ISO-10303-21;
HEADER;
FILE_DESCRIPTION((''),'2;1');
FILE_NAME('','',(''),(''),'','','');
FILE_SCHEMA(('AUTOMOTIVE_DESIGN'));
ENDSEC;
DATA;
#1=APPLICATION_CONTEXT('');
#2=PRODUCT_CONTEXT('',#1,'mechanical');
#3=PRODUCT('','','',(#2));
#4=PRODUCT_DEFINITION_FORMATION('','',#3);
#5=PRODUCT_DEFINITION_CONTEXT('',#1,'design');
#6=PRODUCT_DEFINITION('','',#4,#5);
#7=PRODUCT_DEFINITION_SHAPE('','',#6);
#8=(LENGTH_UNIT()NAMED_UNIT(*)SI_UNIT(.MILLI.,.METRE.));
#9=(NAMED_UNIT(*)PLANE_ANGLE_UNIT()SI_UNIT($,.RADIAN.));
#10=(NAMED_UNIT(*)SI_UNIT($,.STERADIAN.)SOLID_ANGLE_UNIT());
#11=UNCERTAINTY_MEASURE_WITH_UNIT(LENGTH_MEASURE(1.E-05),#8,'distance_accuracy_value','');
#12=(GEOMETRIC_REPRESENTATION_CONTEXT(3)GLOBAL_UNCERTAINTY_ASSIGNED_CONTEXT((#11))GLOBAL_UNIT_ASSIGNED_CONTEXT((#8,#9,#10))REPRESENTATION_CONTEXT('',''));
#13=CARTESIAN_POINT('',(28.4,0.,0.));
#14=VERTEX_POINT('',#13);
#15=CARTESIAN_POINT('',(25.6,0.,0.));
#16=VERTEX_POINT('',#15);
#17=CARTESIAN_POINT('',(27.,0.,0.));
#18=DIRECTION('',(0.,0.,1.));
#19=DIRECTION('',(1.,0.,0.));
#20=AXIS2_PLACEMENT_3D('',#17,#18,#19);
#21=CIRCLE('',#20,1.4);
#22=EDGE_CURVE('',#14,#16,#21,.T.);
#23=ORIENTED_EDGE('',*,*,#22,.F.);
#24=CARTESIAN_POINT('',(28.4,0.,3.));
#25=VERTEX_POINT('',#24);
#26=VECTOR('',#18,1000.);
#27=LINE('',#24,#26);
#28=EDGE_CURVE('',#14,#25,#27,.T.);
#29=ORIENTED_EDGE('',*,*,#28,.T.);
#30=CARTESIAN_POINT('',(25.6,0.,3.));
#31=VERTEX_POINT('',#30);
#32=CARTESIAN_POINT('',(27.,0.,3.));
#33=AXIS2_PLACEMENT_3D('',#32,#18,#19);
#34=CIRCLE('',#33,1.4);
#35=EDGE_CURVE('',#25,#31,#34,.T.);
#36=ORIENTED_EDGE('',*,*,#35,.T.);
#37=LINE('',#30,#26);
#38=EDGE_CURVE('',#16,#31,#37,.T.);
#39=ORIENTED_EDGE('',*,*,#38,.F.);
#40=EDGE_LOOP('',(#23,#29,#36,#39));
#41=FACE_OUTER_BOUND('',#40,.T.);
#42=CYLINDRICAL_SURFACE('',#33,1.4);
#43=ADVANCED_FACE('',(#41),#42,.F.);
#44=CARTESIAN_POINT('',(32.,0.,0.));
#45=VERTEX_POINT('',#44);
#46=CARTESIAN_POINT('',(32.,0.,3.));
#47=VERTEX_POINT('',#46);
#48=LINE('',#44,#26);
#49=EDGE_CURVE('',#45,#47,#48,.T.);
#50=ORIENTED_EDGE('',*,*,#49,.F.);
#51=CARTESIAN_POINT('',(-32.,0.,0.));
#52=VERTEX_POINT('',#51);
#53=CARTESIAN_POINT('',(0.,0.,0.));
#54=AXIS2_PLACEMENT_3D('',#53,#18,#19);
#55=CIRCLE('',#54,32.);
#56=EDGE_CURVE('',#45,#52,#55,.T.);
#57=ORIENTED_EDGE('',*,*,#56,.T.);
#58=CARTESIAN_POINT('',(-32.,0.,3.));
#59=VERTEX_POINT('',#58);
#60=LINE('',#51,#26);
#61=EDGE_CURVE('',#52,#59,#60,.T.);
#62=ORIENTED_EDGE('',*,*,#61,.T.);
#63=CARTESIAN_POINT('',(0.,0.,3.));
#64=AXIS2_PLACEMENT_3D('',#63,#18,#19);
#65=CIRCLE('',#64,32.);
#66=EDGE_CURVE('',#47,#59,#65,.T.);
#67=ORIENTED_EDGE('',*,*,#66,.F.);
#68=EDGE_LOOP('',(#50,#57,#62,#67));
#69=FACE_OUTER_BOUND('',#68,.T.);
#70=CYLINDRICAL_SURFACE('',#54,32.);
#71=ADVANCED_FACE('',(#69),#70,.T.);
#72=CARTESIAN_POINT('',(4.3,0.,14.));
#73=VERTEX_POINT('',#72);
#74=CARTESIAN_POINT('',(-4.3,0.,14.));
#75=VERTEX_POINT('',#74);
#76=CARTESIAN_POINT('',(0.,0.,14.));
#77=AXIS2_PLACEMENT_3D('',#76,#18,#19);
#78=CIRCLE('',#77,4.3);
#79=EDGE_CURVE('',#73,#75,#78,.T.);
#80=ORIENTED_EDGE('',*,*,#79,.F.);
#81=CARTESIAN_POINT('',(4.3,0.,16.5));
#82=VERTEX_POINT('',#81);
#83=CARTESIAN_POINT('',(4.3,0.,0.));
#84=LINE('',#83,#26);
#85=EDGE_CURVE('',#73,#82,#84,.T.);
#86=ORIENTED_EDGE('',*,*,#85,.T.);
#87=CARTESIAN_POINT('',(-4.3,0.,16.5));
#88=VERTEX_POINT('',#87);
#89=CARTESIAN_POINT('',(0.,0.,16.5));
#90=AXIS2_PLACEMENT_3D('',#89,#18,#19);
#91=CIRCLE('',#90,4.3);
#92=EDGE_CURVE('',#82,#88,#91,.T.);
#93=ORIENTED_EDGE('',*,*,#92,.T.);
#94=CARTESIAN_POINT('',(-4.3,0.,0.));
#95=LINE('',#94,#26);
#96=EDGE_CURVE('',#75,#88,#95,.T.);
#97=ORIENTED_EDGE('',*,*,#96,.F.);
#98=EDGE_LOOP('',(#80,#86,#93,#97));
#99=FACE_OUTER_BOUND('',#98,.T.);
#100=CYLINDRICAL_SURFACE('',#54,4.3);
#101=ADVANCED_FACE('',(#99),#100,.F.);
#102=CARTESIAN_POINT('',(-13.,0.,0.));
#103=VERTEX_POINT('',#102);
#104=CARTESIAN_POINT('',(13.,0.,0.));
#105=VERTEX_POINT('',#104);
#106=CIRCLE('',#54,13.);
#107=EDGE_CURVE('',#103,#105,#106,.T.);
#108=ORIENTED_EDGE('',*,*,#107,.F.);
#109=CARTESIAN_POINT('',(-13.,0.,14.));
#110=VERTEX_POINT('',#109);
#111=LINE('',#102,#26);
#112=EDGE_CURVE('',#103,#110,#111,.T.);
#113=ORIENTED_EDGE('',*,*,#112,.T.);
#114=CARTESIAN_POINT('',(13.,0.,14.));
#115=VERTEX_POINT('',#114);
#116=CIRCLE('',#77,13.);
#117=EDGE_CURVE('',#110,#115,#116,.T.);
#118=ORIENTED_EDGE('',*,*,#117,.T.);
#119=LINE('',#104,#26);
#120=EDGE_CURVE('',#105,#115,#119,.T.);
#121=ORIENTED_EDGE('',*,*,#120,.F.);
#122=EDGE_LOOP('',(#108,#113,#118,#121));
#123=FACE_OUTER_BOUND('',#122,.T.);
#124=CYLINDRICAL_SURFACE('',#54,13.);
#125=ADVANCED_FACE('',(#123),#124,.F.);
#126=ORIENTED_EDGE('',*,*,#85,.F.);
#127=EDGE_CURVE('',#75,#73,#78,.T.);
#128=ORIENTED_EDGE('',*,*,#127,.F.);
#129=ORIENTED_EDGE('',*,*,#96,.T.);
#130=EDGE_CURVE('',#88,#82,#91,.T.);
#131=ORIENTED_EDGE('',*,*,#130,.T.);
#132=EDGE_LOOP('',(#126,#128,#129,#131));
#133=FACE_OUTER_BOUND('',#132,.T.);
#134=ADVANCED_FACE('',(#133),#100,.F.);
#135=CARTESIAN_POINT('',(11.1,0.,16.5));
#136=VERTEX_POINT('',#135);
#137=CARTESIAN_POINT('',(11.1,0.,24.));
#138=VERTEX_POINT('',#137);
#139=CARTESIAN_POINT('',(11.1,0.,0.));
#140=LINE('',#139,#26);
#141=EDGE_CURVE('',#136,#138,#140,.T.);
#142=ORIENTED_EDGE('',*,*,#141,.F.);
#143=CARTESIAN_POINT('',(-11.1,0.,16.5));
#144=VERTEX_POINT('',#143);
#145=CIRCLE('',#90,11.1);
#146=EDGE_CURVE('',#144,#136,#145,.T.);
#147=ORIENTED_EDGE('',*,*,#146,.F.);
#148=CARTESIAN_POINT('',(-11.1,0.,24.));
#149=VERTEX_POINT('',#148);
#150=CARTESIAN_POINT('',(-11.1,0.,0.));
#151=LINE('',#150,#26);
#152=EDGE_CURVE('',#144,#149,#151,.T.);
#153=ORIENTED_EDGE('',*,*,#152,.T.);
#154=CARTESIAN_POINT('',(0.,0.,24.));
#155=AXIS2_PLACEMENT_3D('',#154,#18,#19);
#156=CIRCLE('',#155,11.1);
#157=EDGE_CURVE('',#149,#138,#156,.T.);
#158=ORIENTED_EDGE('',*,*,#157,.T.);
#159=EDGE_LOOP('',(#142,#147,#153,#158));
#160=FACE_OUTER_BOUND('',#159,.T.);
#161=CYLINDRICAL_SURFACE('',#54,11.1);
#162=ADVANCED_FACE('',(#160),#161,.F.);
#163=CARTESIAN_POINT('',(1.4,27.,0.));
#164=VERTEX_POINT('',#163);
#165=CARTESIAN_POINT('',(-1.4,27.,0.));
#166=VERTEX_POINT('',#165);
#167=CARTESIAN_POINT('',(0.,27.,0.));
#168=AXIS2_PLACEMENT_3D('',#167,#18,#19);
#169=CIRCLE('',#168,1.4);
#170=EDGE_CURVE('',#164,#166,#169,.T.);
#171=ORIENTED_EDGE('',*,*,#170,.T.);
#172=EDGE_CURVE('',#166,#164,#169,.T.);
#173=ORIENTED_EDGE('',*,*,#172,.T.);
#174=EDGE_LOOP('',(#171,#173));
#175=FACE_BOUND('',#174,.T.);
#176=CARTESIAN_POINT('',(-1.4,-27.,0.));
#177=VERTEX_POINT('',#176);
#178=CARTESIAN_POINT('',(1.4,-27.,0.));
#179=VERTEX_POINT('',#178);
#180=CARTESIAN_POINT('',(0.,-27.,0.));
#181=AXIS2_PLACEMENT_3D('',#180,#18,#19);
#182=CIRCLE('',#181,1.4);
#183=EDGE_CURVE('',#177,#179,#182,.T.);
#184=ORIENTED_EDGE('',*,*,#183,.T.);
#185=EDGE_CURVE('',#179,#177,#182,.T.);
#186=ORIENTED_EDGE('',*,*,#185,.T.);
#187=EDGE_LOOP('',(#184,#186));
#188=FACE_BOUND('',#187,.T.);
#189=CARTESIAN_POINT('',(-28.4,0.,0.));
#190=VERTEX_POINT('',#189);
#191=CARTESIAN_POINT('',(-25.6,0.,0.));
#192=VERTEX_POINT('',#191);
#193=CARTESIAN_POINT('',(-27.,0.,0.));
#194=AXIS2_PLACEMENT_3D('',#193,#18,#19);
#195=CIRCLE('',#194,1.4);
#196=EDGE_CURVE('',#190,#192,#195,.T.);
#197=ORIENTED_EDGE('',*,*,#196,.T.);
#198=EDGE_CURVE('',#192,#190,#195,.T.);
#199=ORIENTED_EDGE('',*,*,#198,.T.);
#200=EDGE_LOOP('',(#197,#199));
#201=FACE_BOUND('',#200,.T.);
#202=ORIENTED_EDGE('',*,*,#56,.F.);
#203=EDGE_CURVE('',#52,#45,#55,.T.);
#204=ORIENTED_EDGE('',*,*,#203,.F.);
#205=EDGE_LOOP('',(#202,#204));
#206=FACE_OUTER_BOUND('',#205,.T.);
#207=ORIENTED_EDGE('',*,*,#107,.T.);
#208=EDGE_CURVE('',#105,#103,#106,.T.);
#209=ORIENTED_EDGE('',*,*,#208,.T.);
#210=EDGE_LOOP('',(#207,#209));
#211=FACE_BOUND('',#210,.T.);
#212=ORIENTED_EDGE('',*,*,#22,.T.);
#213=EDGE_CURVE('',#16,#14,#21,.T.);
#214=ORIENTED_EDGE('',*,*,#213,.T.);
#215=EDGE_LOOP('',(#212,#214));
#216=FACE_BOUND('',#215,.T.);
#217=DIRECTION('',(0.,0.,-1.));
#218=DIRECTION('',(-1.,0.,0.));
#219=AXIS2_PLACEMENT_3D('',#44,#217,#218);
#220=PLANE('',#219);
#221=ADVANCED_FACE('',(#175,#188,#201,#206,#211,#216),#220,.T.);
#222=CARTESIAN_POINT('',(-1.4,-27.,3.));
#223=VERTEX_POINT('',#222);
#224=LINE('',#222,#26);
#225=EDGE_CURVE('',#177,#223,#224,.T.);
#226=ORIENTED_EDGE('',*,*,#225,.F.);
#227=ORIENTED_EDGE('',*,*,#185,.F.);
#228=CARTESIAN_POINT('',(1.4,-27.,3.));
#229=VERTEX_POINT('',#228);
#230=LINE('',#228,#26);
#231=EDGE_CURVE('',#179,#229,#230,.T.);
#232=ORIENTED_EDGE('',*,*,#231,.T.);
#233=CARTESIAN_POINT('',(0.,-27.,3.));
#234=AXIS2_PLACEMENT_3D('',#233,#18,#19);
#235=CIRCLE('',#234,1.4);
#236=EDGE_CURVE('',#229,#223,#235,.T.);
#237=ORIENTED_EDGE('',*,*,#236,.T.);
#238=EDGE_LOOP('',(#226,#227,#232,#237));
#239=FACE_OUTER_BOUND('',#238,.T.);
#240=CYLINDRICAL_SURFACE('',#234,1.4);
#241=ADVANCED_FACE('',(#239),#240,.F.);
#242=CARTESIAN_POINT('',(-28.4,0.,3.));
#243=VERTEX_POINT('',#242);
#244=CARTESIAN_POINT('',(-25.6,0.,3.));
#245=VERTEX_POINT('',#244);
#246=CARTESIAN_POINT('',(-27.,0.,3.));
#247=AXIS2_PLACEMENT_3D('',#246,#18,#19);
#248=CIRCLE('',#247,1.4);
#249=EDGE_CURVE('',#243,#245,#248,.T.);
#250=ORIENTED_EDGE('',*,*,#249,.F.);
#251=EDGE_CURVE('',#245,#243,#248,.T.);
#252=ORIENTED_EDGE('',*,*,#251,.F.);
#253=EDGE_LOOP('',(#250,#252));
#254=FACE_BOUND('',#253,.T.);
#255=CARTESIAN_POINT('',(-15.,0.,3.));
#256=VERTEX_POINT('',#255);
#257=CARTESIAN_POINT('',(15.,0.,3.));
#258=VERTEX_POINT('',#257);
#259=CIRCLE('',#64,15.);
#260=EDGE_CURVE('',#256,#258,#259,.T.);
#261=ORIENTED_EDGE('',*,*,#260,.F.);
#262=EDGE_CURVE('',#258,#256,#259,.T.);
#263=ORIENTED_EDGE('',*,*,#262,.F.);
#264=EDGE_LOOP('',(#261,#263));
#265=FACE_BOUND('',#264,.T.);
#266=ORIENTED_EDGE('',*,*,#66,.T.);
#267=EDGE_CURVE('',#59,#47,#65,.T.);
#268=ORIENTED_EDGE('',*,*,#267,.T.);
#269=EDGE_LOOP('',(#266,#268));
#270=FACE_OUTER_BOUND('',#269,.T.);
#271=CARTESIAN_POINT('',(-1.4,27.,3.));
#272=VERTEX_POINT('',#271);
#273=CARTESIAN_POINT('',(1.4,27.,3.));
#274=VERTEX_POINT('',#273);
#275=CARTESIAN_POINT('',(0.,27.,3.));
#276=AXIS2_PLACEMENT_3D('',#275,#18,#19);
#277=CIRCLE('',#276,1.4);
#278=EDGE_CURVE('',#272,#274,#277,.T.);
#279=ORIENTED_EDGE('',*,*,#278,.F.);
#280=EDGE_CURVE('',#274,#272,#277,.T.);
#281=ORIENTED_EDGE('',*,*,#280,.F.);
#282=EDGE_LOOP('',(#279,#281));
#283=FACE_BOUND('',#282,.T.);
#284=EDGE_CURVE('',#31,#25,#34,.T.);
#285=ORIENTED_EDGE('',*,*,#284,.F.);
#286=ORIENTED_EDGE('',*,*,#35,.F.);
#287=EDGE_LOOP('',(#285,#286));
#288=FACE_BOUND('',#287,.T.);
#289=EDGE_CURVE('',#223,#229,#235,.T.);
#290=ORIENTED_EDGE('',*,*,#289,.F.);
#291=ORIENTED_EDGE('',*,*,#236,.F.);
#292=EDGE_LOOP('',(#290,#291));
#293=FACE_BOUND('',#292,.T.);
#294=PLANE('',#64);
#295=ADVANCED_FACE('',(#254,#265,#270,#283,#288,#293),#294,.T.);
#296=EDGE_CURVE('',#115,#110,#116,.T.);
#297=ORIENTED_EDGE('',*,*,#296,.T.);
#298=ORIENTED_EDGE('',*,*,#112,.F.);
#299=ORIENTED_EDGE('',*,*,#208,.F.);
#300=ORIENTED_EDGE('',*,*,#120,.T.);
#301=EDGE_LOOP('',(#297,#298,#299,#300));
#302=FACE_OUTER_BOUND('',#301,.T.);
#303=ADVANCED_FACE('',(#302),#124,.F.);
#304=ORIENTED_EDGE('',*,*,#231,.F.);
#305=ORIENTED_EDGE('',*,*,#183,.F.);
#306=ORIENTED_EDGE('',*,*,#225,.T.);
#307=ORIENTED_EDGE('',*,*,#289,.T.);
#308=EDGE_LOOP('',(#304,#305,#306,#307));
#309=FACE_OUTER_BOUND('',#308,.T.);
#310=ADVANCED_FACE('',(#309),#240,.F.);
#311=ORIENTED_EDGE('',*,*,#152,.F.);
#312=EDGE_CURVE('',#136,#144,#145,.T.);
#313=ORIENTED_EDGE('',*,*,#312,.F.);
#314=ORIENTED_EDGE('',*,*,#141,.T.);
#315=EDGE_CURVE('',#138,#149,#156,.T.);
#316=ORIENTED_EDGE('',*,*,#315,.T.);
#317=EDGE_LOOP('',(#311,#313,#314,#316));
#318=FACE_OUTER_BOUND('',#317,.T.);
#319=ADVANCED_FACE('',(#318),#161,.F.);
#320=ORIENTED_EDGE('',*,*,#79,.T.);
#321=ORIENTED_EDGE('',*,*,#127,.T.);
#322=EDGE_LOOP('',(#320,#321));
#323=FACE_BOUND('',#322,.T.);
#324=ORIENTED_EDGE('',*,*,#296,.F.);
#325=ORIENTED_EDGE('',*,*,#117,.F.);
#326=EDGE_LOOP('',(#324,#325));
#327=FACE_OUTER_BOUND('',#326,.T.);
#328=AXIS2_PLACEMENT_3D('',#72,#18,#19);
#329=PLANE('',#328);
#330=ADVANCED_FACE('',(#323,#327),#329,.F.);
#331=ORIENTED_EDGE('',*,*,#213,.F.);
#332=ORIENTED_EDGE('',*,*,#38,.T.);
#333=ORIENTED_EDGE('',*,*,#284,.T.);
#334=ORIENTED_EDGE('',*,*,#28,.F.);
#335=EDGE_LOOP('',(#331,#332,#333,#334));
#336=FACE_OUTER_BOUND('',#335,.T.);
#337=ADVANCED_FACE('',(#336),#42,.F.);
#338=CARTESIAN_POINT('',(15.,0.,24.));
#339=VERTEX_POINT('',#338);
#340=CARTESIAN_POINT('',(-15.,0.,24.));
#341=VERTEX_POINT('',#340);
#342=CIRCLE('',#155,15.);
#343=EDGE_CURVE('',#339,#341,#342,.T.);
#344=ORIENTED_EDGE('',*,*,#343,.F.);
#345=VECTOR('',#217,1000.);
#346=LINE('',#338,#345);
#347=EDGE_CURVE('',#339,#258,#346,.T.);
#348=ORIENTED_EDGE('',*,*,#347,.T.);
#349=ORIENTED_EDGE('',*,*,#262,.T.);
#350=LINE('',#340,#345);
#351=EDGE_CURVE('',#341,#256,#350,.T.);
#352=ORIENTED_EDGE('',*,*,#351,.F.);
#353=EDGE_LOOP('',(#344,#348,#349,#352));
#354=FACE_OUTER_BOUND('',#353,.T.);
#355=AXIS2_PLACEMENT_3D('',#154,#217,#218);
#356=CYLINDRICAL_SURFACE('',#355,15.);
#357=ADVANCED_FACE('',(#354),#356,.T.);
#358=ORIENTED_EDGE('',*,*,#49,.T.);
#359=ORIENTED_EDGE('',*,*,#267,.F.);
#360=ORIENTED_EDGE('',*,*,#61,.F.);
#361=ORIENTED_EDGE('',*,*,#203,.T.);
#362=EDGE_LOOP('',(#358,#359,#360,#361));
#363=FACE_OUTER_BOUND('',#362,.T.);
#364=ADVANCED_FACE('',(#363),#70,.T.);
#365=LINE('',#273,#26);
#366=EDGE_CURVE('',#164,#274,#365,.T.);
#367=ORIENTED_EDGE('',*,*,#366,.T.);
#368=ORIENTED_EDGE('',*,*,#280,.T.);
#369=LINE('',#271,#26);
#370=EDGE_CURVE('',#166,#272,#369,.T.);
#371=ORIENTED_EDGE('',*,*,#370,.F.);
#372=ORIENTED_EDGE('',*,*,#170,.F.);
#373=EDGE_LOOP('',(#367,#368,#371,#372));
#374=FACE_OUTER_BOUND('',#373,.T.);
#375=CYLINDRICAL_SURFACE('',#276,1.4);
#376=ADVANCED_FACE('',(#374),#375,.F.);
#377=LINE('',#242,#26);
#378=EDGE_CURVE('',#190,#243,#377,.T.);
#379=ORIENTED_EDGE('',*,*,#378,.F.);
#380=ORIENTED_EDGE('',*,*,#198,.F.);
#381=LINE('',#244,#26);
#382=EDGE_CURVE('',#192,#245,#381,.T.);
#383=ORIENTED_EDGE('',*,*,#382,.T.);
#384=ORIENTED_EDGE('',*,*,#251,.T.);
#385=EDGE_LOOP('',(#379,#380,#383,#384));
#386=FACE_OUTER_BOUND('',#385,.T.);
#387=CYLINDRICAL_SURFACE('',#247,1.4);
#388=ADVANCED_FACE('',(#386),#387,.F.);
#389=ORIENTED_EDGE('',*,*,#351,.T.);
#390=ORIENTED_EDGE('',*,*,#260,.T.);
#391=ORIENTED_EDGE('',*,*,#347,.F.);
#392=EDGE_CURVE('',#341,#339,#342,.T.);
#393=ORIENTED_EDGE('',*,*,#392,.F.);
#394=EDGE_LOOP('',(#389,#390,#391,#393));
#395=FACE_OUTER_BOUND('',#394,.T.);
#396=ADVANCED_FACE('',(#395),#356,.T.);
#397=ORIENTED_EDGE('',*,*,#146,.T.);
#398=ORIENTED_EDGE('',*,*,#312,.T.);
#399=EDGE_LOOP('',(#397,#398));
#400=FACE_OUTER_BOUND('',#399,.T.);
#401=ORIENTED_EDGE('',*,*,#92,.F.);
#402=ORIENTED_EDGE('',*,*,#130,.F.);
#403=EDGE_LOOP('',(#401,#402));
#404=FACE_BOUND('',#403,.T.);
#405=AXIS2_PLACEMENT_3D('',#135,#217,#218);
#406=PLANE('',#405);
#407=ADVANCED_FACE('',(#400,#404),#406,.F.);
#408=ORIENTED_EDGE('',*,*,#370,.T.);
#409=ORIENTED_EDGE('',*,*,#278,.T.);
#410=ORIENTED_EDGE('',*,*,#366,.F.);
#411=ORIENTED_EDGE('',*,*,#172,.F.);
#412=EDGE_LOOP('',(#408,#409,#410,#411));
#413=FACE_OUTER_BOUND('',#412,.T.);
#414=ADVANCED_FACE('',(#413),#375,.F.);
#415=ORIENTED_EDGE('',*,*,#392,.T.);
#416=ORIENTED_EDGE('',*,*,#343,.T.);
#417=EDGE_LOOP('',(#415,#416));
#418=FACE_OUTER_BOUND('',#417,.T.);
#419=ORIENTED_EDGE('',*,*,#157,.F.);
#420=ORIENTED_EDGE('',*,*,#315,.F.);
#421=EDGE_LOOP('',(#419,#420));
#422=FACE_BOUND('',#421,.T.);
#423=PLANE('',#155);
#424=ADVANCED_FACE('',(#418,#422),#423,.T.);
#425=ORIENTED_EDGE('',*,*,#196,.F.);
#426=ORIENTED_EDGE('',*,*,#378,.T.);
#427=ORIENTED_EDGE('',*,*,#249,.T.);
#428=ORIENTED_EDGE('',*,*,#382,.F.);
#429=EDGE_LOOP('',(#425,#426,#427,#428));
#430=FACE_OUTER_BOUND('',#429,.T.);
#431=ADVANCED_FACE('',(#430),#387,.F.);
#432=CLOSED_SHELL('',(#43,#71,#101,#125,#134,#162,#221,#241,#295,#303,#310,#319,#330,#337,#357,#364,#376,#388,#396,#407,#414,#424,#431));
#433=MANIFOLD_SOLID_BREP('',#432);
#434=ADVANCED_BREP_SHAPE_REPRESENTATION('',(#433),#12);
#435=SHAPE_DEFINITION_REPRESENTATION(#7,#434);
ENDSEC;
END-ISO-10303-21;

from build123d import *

# Parameters (mm, degrees)
SKETCH1_W                  = 32
SKETCH1_H                  = 3
SKETCH2_R                  = 15
BOSS_EXTRUDE1_DEPTH        = 21
F_2_8_2_8_DIAMETER_HOLE1_D = 2.8


with BuildPart() as part:
    # Sketch1 → Revolve1 (revolve)
    with BuildSketch(Plane(origin=(0, 0, 0), x_dir=(1, 0, 0), z_dir=(0, 1, 0))):
        with Locations((16, -1.5)):
            Rectangle(SKETCH1_W, SKETCH1_H)
    revolve(axis=Axis((0, 0, 0), (0, 0, 1)))

    # Sketch2 → Boss-Extrude1 (add)
    with BuildSketch(Plane.XY.offset(3)):
        with Locations(Location((0, 0, 0), (0, 0, 180))):
            Circle(SKETCH2_R)
    extrude(amount=BOSS_EXTRUDE1_DEPTH)

    # Sketch3 → Cut-Revolve1 (revolve, cut)
    with BuildSketch(Plane(origin=(0, 0, 0), x_dir=(1, 0, 0), z_dir=(0, 1, 0))):
        Polygon((13, 0), (0, 0), (0, -24), (11.1, -24), (11.1, -16.5), (4.3, -16.5), (4.3, -14), (13, -14), align=None)
    revolve(axis=Axis((0, 0, 0), (0, 0, 1)), mode=Mode.SUBTRACT)

    # Ø2.8 (2.8) Diameter Hole1 (through all)
    with Locations(Plane.XY.offset(3)):
        with Locations((0, 27), (0, -27), (27, 0), (-27, 0)):
            Hole(F_2_8_2_8_DIAMETER_HOLE1_D / 2)


solid = part.part
